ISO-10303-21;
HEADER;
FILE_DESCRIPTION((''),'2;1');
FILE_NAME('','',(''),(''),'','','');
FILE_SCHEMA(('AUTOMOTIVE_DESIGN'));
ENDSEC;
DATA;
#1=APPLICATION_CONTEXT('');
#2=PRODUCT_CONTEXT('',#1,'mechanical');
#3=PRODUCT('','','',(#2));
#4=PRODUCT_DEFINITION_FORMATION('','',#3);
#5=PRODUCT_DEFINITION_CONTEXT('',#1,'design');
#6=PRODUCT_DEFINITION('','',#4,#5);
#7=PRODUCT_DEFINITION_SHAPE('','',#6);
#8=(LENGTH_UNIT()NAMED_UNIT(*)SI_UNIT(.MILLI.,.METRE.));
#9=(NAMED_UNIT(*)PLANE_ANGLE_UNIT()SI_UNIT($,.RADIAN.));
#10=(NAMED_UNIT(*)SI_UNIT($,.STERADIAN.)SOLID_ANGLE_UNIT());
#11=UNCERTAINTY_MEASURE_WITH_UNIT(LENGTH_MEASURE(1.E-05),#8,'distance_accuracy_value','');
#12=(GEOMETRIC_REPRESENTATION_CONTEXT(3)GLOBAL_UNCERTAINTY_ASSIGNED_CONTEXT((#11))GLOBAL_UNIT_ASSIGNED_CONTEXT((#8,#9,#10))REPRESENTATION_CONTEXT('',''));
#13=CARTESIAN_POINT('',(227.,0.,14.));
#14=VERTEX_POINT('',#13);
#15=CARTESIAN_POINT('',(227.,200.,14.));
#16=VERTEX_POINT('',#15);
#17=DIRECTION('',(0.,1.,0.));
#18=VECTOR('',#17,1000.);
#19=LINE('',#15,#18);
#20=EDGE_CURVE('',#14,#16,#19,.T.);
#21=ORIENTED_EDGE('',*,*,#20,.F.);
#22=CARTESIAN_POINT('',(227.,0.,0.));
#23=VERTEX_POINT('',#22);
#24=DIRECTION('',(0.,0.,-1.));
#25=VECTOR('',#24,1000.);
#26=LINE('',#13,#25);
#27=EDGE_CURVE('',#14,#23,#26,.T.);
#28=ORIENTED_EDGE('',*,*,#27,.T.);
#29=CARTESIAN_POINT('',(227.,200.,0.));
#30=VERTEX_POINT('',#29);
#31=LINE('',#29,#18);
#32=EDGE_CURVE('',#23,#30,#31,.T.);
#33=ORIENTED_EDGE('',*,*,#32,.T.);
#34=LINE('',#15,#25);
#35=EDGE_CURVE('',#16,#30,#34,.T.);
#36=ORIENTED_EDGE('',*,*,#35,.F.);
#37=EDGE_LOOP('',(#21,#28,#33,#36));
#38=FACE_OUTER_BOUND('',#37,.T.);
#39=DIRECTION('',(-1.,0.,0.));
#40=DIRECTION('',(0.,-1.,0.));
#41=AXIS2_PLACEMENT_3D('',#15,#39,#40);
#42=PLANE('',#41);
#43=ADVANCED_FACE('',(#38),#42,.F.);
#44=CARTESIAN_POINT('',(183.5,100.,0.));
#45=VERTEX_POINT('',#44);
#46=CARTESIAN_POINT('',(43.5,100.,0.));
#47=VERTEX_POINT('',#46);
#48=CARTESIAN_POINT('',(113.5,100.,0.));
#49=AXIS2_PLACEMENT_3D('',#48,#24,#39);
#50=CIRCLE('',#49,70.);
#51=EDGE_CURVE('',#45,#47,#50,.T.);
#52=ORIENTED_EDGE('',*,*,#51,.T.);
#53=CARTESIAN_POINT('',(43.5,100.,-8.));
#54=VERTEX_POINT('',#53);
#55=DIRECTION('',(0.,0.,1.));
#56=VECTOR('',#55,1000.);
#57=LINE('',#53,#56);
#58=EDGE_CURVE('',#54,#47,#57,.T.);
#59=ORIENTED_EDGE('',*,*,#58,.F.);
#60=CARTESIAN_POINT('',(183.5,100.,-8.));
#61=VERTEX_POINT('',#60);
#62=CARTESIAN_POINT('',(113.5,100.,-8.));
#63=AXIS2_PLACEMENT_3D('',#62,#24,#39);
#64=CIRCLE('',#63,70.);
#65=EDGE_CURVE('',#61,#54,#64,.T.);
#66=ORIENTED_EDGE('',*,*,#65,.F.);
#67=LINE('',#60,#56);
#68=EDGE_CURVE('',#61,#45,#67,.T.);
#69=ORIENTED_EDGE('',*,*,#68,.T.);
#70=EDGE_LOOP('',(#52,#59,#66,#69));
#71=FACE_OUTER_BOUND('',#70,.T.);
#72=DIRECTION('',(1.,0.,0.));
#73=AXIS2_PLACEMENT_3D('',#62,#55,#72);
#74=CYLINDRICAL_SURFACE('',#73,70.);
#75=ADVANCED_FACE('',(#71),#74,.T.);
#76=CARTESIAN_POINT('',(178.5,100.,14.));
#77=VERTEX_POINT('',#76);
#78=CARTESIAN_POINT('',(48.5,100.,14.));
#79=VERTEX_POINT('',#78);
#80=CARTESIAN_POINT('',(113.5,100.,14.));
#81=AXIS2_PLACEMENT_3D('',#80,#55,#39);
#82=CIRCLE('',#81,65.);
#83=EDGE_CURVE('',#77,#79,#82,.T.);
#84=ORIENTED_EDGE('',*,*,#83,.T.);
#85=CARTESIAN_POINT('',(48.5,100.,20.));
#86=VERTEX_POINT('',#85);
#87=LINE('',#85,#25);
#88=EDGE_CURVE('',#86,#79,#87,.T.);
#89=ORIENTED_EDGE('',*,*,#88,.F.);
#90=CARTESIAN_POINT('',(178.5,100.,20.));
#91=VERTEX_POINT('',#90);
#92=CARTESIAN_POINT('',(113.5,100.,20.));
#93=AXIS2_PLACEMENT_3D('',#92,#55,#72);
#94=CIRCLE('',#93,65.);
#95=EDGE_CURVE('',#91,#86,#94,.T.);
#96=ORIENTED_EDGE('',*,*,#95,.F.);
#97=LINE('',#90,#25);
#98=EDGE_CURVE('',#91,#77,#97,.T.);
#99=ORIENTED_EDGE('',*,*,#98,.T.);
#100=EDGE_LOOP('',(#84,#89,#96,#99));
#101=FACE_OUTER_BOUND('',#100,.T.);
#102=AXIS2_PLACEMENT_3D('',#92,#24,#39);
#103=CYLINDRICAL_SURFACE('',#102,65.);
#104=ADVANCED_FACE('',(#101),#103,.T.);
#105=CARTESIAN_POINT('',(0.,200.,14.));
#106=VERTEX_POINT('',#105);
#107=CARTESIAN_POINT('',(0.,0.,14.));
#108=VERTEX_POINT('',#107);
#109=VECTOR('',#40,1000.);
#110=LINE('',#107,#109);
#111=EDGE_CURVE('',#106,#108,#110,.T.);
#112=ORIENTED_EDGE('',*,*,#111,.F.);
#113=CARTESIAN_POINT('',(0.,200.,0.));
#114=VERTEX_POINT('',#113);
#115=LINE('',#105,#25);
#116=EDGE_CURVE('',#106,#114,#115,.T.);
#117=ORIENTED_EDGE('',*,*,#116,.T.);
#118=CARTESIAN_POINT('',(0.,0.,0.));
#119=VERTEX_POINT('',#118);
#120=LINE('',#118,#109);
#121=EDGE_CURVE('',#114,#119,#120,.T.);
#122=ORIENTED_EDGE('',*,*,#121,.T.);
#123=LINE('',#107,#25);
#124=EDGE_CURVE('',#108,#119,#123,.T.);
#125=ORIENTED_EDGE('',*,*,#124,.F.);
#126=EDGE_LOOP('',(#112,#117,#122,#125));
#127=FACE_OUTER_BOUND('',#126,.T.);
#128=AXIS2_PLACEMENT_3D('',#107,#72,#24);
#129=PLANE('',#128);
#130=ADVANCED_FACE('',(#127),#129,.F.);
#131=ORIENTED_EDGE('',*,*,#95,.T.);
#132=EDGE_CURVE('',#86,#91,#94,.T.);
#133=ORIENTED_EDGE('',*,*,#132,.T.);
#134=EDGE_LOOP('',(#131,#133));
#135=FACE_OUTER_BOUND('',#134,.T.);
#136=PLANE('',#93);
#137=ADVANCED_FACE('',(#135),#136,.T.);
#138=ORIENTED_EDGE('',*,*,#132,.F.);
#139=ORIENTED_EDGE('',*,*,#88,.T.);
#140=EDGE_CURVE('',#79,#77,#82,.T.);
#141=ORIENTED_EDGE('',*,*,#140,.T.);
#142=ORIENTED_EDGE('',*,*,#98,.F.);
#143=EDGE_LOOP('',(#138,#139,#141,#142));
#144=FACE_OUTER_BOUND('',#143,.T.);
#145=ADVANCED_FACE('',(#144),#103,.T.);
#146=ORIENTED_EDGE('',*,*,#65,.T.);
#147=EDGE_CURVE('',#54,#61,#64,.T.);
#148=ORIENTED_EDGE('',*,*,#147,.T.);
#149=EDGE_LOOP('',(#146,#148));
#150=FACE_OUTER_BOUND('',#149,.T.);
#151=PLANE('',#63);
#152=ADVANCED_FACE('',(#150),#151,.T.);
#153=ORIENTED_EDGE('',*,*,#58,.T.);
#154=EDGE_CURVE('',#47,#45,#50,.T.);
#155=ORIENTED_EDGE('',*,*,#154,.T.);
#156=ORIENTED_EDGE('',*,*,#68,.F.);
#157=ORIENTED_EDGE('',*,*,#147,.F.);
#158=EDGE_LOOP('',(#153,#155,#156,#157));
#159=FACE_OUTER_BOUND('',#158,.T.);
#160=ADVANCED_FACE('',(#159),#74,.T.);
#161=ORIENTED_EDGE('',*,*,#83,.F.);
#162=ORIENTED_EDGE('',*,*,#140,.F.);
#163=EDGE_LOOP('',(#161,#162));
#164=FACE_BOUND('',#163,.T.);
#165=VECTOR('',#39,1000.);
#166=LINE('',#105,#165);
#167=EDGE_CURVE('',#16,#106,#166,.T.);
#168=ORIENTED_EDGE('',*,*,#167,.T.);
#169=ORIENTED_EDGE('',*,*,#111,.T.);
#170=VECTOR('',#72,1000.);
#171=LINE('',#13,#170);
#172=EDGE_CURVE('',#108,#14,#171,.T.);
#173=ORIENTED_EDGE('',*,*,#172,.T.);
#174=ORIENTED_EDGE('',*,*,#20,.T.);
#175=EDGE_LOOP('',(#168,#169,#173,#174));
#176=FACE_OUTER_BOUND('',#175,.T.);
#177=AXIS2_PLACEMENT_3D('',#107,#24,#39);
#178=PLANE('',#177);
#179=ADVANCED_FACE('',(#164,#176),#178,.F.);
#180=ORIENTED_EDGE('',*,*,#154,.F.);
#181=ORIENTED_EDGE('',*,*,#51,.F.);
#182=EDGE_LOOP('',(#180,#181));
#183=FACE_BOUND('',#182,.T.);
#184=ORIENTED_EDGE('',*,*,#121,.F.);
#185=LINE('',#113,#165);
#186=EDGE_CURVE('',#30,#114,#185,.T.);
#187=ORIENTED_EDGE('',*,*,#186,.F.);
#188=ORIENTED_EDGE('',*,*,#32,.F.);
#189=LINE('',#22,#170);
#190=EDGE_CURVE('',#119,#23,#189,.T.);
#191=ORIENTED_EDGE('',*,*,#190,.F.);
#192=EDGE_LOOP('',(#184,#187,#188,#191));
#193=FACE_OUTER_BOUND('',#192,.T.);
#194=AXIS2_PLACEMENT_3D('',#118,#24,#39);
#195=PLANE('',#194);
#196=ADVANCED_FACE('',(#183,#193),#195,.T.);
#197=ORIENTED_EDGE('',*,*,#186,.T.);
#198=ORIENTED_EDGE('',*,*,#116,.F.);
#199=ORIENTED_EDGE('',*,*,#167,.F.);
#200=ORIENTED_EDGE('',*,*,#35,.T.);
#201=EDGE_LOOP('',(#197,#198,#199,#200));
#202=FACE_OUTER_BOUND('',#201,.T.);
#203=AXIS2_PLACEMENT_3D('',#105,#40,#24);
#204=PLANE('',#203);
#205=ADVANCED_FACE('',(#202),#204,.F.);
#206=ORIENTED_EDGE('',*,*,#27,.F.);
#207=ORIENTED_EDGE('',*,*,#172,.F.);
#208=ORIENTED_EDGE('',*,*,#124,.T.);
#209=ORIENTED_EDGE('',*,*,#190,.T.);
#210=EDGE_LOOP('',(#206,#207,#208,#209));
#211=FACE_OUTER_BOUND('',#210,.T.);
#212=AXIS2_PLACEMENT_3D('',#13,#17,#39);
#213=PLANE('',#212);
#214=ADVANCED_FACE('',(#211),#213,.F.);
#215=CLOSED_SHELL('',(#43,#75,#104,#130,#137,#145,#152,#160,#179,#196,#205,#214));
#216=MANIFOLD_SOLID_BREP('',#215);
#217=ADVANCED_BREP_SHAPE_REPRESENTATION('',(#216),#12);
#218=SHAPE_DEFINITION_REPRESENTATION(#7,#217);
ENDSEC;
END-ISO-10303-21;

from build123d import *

# Parameters (mm, degrees)
SKETCH1_W           = 227
SKETCH1_H           = 200
BOSS_EXTRUDE1_DEPTH = 14
SKETCH2_R           = 65
BOSS_EXTRUDE2_DEPTH = 6
SKETCH3_R           = 70
BOSS_EXTRUDE3_DEPTH = 8


with BuildPart() as part:
    # Sketch1 → Boss-Extrude1 (new body)
    with BuildSketch(Plane.XY):
        with Locations((113.5, 100)):
            Rectangle(SKETCH1_W, SKETCH1_H)
    extrude(amount=BOSS_EXTRUDE1_DEPTH)

    # Sketch2 → Boss-Extrude2 (add)
    with BuildSketch(Plane.XY.offset(14)):
        with Locations(Location((113.5, 100, 0), (0, 0, 180))):
            Circle(SKETCH2_R)
    extrude(amount=BOSS_EXTRUDE2_DEPTH)

    # Sketch3 → Boss-Extrude3 (add)
    with BuildSketch(Plane(origin=(0, 0, 0), x_dir=(-1, 0, 0), z_dir=(0, 0, -1))):
        with Locations((-113.5, 100)):
            Circle(SKETCH3_R)
    extrude(amount=BOSS_EXTRUDE3_DEPTH)


solid = part.part
